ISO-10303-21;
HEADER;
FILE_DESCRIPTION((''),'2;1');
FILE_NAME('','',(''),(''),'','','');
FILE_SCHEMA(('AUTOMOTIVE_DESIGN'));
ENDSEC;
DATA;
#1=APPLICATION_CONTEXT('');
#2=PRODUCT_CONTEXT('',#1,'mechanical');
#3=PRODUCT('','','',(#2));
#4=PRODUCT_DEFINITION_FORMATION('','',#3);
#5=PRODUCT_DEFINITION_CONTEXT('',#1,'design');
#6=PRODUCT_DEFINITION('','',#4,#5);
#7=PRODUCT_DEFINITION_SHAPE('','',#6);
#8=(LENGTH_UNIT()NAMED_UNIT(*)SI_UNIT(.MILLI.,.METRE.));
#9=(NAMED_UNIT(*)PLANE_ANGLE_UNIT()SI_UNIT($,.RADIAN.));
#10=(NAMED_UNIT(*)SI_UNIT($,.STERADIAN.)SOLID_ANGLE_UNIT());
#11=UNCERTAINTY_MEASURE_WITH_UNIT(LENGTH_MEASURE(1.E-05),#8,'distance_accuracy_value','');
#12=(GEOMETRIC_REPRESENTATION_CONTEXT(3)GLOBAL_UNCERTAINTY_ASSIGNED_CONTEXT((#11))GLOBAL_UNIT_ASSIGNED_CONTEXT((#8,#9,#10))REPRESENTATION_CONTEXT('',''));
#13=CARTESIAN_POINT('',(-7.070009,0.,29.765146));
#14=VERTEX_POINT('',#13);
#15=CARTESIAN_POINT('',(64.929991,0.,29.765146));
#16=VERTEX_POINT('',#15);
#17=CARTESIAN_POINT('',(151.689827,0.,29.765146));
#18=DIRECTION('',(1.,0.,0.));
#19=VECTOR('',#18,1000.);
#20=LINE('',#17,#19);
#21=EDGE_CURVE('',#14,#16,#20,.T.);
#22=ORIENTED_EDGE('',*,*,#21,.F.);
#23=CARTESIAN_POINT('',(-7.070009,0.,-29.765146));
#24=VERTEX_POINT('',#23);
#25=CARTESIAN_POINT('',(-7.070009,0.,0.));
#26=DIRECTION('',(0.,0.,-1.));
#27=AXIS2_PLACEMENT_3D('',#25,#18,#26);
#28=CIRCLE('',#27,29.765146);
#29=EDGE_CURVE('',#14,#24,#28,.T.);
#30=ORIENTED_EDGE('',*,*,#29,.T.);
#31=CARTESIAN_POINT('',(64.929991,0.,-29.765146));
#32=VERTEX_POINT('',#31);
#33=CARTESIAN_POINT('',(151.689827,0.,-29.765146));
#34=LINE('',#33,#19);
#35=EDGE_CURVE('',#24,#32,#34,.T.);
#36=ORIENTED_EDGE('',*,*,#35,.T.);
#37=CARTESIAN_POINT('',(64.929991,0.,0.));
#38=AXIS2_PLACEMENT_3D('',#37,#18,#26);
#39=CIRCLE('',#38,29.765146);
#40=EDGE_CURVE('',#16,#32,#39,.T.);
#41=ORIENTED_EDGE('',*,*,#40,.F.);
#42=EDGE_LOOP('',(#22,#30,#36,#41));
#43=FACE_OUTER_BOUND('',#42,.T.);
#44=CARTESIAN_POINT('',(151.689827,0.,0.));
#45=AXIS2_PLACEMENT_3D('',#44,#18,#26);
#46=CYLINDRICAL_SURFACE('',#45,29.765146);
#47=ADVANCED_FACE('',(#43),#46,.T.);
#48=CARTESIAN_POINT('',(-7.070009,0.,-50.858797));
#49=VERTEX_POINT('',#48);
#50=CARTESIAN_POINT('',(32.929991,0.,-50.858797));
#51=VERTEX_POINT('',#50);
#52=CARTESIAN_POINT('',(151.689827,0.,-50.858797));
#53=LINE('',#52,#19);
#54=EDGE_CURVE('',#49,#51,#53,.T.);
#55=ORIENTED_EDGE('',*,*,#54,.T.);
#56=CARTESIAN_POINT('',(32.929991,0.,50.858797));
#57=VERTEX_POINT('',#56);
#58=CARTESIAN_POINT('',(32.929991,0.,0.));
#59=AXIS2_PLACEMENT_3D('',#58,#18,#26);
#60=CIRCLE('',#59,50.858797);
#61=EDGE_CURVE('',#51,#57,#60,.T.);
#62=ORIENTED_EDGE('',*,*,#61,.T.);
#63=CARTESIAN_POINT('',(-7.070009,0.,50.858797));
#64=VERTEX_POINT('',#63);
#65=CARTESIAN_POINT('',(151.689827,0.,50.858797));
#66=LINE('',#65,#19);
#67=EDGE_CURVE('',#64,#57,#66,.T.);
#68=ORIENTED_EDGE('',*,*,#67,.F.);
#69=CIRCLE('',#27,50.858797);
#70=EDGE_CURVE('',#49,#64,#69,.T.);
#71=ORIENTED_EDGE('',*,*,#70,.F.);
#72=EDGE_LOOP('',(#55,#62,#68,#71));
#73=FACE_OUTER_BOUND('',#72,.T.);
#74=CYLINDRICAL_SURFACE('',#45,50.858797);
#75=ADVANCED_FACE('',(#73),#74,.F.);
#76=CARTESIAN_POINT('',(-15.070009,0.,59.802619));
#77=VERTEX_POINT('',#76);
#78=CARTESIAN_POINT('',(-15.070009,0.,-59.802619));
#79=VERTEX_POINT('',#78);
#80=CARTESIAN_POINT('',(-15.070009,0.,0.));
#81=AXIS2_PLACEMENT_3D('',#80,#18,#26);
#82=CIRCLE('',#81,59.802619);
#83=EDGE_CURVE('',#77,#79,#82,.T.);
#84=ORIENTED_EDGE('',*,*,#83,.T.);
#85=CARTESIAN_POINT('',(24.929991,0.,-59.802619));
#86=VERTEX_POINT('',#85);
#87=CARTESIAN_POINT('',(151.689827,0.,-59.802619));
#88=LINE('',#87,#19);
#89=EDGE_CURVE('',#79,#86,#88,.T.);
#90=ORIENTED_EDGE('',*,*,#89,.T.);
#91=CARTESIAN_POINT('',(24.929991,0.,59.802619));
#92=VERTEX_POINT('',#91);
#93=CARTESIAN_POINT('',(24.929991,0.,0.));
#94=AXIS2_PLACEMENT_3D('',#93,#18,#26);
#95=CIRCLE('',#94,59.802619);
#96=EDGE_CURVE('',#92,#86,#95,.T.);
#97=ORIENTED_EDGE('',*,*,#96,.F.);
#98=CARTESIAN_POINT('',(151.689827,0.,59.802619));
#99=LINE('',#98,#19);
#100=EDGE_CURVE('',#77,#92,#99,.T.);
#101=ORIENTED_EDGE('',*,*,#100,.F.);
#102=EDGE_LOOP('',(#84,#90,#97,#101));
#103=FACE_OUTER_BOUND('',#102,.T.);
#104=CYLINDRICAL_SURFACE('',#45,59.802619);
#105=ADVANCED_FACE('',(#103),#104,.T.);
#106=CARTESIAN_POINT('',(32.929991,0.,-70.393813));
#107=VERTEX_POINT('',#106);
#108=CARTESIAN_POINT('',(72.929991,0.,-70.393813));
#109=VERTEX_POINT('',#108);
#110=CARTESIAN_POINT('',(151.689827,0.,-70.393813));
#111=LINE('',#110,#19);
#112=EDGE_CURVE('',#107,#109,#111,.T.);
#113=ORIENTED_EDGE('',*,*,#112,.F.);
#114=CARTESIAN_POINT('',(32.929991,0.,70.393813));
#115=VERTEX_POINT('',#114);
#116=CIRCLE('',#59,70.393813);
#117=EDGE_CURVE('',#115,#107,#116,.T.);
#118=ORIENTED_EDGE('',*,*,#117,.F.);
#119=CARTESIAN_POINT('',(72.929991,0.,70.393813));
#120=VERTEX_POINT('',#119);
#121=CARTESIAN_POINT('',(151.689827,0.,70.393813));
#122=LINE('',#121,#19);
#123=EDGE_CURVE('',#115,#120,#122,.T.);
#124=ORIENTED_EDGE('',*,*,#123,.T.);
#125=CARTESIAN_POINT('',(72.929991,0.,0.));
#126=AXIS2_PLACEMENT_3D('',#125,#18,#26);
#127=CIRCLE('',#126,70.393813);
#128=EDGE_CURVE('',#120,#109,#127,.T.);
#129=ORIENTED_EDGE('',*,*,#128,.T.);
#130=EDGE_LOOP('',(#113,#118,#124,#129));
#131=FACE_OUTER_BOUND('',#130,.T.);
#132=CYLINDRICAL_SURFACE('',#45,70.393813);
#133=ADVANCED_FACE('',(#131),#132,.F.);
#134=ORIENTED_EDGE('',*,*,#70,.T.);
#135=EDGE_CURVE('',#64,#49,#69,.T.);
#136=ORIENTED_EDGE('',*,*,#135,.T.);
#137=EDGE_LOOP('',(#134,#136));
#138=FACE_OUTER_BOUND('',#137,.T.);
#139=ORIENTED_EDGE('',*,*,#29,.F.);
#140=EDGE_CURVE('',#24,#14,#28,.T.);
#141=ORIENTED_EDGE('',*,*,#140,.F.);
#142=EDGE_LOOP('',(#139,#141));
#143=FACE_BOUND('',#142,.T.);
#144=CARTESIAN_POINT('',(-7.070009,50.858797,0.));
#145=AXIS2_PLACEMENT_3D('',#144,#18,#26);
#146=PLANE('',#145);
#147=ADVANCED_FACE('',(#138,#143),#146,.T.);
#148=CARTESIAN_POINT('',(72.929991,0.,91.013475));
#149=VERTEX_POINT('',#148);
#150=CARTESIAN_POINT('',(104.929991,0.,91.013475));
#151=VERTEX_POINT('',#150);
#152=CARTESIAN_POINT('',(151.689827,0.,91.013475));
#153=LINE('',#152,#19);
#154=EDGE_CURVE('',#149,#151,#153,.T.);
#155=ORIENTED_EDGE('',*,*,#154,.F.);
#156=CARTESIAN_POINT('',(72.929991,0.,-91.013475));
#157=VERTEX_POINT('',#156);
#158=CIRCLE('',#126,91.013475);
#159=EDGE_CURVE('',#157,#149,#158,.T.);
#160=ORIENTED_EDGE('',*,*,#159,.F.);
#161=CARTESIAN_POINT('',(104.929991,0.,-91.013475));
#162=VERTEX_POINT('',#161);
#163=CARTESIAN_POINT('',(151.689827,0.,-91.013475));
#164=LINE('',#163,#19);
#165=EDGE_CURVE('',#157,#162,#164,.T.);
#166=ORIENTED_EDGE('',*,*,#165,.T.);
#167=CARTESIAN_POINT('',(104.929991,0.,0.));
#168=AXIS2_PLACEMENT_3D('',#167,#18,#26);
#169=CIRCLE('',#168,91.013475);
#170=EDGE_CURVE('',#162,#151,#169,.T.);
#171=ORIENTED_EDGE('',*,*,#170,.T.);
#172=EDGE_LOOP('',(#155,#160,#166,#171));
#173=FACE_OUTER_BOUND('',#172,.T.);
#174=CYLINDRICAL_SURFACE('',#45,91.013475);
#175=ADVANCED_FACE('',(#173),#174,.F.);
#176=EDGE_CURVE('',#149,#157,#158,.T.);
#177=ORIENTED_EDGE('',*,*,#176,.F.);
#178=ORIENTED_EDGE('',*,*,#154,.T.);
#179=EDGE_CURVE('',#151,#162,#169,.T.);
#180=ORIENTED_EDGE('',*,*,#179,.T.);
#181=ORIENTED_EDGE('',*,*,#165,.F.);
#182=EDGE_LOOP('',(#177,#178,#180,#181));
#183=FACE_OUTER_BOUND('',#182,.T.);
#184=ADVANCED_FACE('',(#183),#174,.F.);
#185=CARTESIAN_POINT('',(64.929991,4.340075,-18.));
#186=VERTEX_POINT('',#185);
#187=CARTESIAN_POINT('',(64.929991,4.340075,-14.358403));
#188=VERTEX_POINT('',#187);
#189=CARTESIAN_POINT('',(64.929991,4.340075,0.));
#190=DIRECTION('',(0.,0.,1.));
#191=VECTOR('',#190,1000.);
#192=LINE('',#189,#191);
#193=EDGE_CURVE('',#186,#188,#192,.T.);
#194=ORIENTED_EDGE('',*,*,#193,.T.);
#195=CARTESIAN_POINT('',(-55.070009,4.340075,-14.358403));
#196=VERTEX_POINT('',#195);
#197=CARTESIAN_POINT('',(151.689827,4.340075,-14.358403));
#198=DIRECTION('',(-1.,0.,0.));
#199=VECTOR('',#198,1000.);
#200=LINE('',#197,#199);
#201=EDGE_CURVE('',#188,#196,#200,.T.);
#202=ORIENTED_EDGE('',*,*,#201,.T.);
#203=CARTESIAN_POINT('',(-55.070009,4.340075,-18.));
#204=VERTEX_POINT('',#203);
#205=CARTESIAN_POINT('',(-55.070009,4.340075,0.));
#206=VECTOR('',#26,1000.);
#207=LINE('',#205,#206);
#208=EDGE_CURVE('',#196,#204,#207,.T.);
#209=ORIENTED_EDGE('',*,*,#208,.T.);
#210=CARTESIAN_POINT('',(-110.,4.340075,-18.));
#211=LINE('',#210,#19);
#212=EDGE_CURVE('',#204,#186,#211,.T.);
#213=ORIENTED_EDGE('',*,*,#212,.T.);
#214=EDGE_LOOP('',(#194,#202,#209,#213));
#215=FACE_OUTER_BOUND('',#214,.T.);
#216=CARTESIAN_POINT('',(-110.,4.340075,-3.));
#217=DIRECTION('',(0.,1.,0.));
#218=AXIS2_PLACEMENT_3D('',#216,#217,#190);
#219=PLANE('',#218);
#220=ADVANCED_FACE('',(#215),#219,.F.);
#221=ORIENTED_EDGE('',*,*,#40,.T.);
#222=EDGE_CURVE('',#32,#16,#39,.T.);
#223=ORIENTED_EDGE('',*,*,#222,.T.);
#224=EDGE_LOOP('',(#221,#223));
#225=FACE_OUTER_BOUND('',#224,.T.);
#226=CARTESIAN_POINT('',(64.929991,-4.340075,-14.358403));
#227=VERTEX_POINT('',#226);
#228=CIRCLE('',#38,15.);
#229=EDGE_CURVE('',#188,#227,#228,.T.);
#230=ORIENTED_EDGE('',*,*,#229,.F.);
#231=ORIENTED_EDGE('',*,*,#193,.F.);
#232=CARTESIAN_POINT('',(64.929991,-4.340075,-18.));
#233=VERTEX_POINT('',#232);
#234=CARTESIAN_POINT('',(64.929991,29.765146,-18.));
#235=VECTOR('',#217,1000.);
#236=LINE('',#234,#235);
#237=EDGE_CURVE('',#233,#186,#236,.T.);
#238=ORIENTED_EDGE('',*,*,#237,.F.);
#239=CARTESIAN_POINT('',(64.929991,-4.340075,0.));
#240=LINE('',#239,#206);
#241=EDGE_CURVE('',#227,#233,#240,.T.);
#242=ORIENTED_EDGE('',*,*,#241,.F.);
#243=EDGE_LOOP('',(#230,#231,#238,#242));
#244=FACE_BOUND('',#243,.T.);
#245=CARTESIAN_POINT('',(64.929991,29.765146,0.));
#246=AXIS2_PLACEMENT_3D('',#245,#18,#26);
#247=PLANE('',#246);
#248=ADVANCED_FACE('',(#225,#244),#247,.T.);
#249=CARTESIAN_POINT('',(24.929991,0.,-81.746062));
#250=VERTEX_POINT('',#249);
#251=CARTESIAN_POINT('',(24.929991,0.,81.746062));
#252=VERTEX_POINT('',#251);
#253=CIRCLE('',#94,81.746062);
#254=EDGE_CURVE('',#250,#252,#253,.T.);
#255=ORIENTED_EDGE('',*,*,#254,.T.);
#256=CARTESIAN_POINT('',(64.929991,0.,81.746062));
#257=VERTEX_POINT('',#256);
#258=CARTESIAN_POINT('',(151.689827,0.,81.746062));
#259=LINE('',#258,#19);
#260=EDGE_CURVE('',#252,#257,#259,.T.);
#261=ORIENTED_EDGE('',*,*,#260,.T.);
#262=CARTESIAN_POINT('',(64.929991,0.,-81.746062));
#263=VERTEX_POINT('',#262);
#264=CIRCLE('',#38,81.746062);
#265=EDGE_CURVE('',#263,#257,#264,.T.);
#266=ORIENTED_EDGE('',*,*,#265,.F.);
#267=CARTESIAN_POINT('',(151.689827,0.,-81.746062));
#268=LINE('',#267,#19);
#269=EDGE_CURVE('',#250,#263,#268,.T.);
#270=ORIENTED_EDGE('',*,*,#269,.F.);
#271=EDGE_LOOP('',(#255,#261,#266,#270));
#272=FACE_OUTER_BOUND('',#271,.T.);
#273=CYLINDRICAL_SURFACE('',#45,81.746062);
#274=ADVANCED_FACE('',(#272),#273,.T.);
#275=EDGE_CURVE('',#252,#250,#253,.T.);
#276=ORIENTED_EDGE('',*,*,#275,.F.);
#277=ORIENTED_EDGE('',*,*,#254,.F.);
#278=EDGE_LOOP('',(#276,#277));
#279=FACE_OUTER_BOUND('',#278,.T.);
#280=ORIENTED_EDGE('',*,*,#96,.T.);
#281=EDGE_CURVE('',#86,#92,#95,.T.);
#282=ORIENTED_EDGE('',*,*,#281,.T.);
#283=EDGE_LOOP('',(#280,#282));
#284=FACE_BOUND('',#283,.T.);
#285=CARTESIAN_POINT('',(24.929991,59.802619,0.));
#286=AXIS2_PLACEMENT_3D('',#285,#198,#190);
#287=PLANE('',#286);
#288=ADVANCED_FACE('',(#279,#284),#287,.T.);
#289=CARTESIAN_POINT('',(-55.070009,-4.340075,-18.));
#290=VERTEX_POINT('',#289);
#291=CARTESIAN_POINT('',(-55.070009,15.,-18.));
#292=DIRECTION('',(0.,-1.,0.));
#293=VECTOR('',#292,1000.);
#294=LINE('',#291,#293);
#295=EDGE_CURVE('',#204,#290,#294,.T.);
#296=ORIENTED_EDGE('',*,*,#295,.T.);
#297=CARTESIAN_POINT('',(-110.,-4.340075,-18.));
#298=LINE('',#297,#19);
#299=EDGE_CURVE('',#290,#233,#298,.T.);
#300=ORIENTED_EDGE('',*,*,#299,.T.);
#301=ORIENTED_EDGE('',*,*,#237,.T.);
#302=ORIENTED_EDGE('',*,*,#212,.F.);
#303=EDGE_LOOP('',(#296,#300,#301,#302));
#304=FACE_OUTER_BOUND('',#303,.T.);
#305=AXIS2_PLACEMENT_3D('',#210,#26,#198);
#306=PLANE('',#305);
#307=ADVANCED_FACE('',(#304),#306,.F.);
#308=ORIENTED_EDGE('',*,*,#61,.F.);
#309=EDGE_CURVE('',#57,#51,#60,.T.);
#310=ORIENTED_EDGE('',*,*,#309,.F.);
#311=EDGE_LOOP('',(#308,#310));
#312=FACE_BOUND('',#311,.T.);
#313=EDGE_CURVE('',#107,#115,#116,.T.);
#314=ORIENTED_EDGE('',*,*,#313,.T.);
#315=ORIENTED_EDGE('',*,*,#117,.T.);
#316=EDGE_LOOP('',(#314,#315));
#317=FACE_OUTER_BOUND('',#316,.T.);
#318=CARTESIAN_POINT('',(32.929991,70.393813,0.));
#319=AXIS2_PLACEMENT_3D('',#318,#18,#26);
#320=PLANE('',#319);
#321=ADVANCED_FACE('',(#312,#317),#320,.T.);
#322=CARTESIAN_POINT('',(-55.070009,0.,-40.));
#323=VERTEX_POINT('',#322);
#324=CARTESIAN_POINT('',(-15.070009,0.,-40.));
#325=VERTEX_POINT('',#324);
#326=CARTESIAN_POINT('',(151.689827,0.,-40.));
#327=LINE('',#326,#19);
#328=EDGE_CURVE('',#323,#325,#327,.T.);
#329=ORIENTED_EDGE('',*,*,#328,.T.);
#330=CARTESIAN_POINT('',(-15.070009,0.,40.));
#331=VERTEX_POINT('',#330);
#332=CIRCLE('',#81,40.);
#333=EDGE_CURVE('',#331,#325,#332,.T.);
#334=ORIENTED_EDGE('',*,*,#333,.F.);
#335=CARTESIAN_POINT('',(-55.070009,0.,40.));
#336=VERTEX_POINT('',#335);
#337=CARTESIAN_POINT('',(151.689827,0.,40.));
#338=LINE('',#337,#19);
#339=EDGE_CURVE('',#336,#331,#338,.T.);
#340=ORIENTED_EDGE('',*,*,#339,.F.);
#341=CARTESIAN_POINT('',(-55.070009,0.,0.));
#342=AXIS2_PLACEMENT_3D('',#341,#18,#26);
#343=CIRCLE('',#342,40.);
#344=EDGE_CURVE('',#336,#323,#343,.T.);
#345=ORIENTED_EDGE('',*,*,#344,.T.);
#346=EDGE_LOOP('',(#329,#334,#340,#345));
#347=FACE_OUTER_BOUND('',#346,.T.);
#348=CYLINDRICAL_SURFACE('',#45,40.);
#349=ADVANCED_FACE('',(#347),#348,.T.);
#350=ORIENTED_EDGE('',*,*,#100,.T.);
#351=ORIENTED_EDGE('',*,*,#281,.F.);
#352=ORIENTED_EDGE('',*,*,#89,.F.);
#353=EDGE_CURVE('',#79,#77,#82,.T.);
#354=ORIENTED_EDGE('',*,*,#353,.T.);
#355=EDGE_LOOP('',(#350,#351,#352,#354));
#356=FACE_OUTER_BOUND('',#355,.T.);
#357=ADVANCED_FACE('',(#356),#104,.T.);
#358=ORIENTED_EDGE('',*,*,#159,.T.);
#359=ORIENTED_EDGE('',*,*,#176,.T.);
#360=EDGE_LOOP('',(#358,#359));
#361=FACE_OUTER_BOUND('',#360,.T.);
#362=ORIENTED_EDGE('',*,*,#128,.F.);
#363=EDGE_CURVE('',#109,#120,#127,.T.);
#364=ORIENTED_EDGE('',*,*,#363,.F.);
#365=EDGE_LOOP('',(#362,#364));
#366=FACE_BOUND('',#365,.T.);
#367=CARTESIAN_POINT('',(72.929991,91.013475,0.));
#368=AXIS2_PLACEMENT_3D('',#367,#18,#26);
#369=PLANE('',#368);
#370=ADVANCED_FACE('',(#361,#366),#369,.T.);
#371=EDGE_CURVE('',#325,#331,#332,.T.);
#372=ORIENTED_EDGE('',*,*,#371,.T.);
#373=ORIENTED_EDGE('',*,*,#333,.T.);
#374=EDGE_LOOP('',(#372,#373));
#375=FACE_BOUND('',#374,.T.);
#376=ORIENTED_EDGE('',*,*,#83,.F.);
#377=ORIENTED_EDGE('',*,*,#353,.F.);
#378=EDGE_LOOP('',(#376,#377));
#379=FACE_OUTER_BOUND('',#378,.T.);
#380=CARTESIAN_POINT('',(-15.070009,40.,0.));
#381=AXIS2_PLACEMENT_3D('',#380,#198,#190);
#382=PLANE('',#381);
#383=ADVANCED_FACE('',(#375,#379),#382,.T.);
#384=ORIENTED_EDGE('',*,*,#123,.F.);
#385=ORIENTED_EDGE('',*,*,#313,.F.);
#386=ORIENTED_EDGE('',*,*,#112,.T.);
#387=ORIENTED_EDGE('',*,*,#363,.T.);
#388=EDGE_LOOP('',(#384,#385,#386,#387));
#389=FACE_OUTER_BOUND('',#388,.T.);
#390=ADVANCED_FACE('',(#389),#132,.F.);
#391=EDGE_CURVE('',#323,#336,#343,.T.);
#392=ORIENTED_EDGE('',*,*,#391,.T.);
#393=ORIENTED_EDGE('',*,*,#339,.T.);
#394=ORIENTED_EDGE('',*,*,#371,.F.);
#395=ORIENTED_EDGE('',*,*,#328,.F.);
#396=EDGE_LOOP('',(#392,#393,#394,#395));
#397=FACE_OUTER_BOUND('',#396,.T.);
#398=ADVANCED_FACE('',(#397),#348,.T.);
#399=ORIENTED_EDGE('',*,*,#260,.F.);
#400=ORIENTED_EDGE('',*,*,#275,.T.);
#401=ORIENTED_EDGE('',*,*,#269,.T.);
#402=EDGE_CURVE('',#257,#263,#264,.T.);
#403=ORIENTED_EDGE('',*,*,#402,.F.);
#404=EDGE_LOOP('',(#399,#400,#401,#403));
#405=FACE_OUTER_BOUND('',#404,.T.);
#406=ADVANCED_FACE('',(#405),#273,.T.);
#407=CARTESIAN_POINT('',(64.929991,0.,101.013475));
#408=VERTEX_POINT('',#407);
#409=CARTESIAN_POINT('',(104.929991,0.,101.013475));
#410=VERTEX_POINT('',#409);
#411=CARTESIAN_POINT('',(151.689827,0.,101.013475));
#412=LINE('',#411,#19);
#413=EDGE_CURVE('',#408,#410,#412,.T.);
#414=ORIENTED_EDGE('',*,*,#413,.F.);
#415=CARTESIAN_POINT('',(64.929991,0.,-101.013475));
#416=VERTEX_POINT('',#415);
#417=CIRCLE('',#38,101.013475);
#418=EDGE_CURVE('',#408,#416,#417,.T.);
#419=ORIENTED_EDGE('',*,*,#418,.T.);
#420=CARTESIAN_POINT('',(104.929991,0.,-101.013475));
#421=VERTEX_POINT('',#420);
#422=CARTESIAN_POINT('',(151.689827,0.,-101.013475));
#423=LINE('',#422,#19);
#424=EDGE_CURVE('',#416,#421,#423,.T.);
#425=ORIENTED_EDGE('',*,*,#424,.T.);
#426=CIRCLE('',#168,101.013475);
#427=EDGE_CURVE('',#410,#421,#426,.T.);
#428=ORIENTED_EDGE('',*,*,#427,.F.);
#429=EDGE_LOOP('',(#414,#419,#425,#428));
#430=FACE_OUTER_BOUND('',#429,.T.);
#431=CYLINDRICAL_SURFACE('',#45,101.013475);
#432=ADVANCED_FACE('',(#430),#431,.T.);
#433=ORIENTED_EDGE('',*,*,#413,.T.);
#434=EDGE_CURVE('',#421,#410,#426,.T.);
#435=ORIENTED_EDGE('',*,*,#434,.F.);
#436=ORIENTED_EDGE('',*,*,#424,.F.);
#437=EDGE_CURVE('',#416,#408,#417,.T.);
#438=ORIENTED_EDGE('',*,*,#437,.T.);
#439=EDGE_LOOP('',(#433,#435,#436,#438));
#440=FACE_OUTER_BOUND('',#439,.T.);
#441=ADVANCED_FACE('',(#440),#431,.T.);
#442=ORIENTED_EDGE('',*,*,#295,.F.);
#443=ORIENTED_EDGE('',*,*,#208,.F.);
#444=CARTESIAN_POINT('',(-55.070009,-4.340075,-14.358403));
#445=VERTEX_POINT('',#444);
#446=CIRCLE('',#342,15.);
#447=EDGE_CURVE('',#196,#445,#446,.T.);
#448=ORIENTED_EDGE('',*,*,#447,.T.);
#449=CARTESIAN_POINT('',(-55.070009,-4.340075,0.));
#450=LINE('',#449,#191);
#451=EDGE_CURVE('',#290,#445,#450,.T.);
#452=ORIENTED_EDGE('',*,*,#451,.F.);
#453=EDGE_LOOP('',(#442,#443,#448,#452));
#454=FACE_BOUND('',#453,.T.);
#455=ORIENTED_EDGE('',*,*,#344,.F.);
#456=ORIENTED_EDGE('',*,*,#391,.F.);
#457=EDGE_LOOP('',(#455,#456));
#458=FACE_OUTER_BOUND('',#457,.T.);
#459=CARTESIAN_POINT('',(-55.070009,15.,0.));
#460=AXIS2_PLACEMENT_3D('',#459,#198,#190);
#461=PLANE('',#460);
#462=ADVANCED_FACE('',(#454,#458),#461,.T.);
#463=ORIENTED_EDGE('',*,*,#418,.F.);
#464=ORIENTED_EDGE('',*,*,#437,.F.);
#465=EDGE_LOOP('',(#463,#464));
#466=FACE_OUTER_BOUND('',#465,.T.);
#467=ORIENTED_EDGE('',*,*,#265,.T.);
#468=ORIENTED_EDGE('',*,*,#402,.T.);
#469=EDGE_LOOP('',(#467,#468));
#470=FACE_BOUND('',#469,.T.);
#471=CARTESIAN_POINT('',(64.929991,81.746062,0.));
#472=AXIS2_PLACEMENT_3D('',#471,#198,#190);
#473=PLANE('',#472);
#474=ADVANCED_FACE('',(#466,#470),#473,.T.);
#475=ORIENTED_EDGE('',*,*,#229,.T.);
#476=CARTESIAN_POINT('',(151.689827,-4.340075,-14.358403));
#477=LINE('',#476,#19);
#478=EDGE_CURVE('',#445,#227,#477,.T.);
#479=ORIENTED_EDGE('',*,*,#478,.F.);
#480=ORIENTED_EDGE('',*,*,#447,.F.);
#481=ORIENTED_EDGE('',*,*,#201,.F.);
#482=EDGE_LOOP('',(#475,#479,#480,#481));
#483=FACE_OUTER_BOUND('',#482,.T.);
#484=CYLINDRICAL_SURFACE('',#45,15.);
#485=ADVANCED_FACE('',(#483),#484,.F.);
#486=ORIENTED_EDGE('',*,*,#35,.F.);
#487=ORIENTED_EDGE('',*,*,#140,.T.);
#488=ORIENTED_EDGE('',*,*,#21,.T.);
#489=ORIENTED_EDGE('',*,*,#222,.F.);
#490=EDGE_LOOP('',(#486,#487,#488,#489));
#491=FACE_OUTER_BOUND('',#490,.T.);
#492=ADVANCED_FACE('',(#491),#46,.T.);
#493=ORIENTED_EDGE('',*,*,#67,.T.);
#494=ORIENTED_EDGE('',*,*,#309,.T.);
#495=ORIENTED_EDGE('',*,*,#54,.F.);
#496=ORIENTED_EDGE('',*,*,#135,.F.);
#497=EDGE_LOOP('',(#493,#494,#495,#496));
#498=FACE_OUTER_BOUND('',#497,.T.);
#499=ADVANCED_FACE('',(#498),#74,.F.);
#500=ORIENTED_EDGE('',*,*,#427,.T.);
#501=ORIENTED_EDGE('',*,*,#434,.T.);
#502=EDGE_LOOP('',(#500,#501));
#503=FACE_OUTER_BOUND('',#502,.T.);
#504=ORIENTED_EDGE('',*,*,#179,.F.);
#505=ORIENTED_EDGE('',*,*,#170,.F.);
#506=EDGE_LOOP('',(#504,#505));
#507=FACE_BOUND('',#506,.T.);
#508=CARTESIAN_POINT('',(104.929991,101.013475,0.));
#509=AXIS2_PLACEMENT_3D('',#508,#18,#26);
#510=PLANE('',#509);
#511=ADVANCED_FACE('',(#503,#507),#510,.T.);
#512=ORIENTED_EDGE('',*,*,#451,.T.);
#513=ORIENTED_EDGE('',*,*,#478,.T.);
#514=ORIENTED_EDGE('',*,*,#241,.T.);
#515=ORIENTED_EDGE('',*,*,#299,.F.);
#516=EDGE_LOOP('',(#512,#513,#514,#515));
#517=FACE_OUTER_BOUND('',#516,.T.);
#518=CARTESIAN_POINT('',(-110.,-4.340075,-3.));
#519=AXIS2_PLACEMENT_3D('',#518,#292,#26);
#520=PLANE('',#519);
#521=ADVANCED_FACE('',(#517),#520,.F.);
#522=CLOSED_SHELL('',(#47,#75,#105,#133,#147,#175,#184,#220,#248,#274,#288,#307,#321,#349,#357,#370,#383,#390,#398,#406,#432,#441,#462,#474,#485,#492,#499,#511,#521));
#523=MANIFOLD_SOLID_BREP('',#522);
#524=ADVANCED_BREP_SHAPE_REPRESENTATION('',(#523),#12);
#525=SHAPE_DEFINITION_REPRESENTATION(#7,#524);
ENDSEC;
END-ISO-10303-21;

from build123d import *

# Parameters (mm, degrees)
BORE_AND_KEYWAY_PROFILE_W    = 15
BORE_AND_KEYWAY_PROFILE_H    = 8.680150088
SHAFT_BORE_WITH_KEYWAY_DEPTH = 110


with BuildPart() as part:
    # Stepped Pulley Profile → Stepped Pulley Body (revolve)
    with BuildSketch(Plane.XY, mode=Mode.PRIVATE) as stepped_pulley_body_sk:
        Polygon((-55.070008805, 15), (-55.070008805, 40), (-15.070008805, 40), (-15.070008805, 59.802619068), (24.929991195, 59.802619068), (24.929991195, 81.746061819), (64.929991195, 81.746061819), (64.929991195, 101.013474967), (104.929991195, 101.013474967), (104.929991195, 91.013474967), (72.929991195, 91.013474967), (72.929991195, 70.393812799), (32.929991195, 70.393812799), (32.929991195, 50.858796691), (-7.070008805, 50.858796691), (-7.070008805, 29.765145873), (64.929991195, 29.765145873), (64.929991195, 15), align=None)
    revolve(stepped_pulley_body_sk.sketch.rotate(Axis((151.689826596, 0, 0), (-1, 0, 0)), 90), axis=Axis((151.689826596, 0, 0), (-1, 0, 0)))

    # Bore and Keyway Profile → Shaft Bore with Keyway (cut, symmetric)
    with BuildSketch(Plane(origin=(0, 0, 0), x_dir=(0, 0, -1), z_dir=(1, 0, 0))):
        with Locations((10.5, 0)):
            Rectangle(BORE_AND_KEYWAY_PROFILE_W, BORE_AND_KEYWAY_PROFILE_H)
    extrude(amount=SHAFT_BORE_WITH_KEYWAY_DEPTH, both=True, mode=Mode.SUBTRACT)


solid = part.part
